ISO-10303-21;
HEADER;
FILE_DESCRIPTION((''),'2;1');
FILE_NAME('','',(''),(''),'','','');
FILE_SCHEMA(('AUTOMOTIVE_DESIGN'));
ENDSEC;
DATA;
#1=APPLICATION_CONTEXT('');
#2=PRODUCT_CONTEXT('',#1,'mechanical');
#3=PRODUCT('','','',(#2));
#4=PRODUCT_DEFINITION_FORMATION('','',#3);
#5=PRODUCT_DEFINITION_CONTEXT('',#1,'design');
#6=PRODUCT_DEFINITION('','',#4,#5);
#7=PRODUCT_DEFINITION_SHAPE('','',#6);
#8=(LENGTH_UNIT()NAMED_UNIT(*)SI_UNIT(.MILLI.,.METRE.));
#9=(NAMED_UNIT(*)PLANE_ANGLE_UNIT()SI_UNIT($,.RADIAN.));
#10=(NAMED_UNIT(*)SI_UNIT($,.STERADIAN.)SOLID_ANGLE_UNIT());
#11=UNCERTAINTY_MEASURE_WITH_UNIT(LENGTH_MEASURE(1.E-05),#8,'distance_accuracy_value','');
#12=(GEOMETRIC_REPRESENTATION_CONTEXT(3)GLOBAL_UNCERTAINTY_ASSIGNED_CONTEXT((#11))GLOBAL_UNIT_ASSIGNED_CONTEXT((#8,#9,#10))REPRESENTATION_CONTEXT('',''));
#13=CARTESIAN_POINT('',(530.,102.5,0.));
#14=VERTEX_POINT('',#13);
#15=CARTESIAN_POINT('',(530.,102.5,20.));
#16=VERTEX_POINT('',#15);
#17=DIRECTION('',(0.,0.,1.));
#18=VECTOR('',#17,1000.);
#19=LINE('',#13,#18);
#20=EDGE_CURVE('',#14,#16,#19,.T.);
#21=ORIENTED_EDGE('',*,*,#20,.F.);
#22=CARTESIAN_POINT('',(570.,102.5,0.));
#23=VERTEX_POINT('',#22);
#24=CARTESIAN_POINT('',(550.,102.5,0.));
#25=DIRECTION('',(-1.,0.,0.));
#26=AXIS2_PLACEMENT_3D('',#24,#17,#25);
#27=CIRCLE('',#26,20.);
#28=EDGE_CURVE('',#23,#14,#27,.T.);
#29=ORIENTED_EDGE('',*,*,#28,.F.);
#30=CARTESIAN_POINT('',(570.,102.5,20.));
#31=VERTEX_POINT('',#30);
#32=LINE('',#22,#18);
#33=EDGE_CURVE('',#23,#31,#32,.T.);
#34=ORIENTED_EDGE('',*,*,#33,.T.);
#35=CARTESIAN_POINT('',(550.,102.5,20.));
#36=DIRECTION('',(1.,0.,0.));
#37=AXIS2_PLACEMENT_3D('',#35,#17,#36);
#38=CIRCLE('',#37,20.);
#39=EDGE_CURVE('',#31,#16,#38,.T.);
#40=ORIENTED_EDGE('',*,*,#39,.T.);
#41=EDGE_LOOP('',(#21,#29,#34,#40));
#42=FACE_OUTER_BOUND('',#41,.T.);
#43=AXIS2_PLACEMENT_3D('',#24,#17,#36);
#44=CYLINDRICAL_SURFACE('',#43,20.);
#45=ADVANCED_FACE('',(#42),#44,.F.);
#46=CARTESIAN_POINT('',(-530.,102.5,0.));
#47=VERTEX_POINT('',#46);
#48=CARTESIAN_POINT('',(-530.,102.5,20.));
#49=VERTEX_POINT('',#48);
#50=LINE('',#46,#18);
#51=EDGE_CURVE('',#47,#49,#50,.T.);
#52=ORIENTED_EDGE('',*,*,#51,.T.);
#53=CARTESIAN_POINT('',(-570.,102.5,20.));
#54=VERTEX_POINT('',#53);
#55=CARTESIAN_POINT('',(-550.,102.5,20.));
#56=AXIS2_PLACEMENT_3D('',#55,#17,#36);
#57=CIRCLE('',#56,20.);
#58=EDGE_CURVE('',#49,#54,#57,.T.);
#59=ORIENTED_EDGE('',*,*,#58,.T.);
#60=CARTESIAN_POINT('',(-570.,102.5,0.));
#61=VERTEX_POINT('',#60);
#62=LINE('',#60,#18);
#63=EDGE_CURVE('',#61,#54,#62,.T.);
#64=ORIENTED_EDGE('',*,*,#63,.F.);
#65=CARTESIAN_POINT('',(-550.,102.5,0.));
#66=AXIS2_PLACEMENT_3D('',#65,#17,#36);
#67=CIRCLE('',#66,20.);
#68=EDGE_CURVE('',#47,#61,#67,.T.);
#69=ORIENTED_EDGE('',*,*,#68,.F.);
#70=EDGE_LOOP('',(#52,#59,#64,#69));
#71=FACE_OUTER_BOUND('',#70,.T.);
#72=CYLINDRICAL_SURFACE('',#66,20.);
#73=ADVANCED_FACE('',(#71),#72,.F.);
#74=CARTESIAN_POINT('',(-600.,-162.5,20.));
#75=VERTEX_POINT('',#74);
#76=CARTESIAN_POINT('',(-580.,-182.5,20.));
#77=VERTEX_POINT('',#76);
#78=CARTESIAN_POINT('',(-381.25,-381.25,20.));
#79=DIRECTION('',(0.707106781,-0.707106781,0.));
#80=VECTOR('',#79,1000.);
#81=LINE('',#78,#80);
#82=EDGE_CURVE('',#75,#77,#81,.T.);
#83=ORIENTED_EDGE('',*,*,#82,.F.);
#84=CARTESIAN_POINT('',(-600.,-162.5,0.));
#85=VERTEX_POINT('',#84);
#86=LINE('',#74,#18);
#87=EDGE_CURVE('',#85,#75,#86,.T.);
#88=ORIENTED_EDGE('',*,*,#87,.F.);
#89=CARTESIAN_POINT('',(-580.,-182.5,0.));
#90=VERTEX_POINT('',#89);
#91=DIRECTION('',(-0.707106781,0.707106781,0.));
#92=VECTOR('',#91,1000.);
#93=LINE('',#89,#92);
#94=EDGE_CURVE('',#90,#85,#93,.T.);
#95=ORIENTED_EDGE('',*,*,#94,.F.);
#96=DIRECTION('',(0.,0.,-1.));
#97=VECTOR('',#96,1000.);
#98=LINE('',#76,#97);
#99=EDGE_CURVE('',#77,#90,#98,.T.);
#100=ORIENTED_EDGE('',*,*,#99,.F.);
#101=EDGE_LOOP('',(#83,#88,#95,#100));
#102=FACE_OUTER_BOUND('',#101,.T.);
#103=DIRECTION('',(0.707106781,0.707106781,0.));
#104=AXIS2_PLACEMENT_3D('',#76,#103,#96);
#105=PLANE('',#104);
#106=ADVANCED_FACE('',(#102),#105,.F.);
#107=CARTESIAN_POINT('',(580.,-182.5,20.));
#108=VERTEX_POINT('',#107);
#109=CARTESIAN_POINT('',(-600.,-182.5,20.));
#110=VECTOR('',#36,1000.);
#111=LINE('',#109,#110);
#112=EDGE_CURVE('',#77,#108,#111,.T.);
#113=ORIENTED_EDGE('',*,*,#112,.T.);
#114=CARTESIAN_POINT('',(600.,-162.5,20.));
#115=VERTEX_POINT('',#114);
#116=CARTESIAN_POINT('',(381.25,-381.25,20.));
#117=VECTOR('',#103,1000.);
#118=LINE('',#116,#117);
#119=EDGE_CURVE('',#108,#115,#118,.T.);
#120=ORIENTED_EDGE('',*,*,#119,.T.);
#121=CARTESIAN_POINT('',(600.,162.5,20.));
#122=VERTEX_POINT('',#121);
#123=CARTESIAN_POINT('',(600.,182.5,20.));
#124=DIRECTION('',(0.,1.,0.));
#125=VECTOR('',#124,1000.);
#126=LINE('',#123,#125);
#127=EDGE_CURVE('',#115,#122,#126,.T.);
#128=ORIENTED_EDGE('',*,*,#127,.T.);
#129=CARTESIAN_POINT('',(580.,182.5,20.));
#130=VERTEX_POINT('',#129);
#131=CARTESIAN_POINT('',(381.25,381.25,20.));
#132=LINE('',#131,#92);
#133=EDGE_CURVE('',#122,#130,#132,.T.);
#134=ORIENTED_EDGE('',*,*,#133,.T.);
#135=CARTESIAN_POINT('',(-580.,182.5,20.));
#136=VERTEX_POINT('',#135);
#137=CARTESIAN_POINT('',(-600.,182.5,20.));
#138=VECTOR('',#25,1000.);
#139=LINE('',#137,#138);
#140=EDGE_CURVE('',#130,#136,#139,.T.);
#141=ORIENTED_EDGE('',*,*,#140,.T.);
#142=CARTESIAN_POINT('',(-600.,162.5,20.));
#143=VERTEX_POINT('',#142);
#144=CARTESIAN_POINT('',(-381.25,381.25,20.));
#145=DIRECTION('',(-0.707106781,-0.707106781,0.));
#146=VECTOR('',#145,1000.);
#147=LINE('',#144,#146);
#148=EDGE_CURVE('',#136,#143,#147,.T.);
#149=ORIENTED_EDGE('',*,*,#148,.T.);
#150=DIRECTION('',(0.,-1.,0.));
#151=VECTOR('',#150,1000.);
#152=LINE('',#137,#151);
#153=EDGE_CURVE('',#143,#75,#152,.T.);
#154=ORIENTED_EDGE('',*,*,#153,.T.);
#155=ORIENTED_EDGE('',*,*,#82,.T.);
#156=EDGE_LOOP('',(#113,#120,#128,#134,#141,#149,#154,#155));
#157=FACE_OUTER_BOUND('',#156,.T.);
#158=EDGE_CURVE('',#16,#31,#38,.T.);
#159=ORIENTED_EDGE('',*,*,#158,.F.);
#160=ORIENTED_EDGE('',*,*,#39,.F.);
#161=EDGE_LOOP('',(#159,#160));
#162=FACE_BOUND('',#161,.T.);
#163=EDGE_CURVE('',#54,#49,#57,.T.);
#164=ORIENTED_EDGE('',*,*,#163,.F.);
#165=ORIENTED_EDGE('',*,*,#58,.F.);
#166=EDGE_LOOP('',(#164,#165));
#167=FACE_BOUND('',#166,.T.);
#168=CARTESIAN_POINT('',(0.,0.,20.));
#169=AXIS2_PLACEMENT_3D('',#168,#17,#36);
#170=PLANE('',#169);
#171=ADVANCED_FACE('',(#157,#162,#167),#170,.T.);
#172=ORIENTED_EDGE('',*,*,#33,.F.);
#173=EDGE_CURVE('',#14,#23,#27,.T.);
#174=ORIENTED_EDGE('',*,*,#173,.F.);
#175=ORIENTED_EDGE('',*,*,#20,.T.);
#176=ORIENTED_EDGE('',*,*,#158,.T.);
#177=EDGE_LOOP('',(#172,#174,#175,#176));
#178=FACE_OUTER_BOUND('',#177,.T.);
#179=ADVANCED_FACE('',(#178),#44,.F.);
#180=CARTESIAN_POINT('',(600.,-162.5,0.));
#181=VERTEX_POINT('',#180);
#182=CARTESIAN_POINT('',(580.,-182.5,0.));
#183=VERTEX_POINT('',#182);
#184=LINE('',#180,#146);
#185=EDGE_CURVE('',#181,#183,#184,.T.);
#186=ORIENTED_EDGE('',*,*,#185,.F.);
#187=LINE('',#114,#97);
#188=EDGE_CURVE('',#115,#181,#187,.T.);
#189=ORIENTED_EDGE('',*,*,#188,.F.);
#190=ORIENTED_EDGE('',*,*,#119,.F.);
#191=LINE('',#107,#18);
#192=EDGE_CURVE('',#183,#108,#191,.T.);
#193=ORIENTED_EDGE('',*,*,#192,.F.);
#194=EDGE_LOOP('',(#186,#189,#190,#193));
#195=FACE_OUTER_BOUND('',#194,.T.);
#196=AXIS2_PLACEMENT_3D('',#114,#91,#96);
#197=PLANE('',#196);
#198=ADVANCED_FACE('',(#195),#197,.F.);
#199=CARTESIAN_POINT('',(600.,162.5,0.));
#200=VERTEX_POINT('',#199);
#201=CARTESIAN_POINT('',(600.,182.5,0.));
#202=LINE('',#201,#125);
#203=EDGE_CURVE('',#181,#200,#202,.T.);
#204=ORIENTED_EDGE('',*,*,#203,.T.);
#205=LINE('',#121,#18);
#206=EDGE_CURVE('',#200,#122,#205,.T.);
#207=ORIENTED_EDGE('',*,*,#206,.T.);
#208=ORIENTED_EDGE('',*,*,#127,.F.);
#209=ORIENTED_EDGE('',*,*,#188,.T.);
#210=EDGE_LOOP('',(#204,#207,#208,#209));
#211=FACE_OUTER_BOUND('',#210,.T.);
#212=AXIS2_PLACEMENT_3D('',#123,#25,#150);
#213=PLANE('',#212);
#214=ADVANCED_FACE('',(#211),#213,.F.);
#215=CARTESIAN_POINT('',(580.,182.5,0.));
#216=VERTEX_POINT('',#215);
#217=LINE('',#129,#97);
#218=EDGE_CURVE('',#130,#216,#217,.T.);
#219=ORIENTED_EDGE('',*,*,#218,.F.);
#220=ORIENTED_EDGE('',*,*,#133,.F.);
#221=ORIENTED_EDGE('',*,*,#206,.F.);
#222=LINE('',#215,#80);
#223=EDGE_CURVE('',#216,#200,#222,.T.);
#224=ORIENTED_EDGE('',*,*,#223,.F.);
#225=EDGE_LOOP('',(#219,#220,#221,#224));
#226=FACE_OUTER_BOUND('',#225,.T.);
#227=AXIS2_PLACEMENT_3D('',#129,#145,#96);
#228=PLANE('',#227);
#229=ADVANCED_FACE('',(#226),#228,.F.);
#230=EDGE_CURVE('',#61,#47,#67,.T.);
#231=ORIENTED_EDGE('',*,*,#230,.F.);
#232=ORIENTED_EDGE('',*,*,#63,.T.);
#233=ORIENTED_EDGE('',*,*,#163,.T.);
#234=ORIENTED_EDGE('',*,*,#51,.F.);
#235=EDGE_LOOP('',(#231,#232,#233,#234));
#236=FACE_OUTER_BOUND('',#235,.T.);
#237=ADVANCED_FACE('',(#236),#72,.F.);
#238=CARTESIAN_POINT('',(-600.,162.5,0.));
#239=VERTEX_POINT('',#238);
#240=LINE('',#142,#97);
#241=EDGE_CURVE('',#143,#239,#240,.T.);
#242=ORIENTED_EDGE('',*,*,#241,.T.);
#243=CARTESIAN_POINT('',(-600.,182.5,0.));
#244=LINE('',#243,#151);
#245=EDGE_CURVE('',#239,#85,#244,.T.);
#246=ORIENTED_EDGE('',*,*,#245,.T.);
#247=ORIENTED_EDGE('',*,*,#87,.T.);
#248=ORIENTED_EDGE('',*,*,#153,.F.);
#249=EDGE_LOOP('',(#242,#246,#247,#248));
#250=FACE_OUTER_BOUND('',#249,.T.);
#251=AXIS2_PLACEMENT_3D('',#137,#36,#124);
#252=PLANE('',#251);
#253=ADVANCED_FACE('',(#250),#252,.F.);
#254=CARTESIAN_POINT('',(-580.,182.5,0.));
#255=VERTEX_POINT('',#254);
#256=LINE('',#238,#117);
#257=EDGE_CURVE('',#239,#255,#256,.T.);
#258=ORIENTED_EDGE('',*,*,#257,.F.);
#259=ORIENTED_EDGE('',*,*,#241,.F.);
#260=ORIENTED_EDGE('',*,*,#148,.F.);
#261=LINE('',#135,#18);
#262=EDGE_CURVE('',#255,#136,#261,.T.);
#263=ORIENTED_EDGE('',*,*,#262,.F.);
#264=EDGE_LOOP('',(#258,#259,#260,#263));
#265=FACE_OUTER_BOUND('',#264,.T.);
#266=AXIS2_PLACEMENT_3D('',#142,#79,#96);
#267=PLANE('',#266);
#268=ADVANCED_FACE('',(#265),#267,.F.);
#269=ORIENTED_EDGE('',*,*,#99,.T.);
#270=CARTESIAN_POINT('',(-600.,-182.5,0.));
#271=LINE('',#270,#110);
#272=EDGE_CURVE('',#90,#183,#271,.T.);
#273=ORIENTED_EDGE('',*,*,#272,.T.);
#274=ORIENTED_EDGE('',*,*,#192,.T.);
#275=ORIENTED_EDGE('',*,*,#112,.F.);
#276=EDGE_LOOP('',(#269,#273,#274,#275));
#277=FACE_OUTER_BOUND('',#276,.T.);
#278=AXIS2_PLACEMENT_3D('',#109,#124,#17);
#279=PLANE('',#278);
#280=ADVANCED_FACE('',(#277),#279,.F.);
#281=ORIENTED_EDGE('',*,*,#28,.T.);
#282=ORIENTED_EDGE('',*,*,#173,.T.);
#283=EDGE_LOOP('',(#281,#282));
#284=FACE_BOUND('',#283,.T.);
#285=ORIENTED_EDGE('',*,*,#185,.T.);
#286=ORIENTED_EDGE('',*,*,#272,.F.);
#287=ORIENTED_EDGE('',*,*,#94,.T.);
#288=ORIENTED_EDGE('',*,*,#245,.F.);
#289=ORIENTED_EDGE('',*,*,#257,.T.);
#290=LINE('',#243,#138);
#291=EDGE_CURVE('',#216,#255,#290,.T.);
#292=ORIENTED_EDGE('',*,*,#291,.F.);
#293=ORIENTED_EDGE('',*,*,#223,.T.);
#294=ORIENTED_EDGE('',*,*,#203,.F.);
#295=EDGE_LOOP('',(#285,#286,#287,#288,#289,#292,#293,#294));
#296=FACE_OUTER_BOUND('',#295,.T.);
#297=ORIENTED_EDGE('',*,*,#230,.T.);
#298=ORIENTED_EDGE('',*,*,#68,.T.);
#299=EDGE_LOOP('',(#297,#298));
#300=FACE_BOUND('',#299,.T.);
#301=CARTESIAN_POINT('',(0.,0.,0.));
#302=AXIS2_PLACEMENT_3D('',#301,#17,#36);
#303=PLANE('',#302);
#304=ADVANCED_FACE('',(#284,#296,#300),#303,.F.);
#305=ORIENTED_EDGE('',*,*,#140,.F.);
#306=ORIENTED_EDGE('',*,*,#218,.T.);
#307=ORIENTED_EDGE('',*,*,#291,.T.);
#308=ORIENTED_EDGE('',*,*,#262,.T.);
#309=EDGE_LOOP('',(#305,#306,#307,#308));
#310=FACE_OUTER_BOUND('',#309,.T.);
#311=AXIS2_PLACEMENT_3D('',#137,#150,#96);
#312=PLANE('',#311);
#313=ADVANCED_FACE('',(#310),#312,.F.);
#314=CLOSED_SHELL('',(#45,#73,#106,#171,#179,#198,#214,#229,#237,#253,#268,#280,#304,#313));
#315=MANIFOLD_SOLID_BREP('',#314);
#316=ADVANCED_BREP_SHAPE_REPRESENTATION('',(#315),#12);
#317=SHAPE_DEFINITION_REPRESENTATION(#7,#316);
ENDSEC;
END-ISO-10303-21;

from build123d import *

# Parameters (mm, degrees)
SKETCH1_W               = 1200
SKETCH1_H               = 365
BOSS_EXTRUDE1_DEPTH     = 20
CUT_EXTRUDE1_DEPTH      = 628.460158098
CUT_EXTRUDE1_DEPTH_BACK = 628.460158098
SKETCH2_R               = 20
CHAMFER1_SIZE           = 20
CHAMFER2_SIZE           = 20


with BuildPart() as part:
    # Sketch1 → Boss-Extrude1 (new body)
    with BuildSketch(Plane.XY):
        Rectangle(SKETCH1_W, SKETCH1_H)
    extrude(amount=BOSS_EXTRUDE1_DEPTH)

    # Sketch2 → Cut-Extrude1 (cut, two sides: drawn at the far end of the back side and taken through both)
    with BuildSketch(Plane.XY.offset(20).offset(-CUT_EXTRUDE1_DEPTH_BACK)):
        with Locations((-550, 102.5)):
            Circle(SKETCH2_R)
        with Locations((550, 102.5)):
            Circle(SKETCH2_R)
    extrude(amount=CUT_EXTRUDE1_DEPTH + CUT_EXTRUDE1_DEPTH_BACK, mode=Mode.SUBTRACT)

    # Chamfer1
    chamfer1_edges = [part.edges().sort_by_distance(p)[0] for p in [
        (-600, 182.5, 10),
        (600, 182.5, 10),
    ]]
    chamfer(chamfer1_edges, length=CHAMFER1_SIZE)

    # Chamfer2
    chamfer2_edges = [part.edges().sort_by_distance(p)[0] for p in [
        (600, -182.5, 10),
        (-600, -182.5, 10),
    ]]
    chamfer(chamfer2_edges, length=CHAMFER2_SIZE)


solid = part.part
